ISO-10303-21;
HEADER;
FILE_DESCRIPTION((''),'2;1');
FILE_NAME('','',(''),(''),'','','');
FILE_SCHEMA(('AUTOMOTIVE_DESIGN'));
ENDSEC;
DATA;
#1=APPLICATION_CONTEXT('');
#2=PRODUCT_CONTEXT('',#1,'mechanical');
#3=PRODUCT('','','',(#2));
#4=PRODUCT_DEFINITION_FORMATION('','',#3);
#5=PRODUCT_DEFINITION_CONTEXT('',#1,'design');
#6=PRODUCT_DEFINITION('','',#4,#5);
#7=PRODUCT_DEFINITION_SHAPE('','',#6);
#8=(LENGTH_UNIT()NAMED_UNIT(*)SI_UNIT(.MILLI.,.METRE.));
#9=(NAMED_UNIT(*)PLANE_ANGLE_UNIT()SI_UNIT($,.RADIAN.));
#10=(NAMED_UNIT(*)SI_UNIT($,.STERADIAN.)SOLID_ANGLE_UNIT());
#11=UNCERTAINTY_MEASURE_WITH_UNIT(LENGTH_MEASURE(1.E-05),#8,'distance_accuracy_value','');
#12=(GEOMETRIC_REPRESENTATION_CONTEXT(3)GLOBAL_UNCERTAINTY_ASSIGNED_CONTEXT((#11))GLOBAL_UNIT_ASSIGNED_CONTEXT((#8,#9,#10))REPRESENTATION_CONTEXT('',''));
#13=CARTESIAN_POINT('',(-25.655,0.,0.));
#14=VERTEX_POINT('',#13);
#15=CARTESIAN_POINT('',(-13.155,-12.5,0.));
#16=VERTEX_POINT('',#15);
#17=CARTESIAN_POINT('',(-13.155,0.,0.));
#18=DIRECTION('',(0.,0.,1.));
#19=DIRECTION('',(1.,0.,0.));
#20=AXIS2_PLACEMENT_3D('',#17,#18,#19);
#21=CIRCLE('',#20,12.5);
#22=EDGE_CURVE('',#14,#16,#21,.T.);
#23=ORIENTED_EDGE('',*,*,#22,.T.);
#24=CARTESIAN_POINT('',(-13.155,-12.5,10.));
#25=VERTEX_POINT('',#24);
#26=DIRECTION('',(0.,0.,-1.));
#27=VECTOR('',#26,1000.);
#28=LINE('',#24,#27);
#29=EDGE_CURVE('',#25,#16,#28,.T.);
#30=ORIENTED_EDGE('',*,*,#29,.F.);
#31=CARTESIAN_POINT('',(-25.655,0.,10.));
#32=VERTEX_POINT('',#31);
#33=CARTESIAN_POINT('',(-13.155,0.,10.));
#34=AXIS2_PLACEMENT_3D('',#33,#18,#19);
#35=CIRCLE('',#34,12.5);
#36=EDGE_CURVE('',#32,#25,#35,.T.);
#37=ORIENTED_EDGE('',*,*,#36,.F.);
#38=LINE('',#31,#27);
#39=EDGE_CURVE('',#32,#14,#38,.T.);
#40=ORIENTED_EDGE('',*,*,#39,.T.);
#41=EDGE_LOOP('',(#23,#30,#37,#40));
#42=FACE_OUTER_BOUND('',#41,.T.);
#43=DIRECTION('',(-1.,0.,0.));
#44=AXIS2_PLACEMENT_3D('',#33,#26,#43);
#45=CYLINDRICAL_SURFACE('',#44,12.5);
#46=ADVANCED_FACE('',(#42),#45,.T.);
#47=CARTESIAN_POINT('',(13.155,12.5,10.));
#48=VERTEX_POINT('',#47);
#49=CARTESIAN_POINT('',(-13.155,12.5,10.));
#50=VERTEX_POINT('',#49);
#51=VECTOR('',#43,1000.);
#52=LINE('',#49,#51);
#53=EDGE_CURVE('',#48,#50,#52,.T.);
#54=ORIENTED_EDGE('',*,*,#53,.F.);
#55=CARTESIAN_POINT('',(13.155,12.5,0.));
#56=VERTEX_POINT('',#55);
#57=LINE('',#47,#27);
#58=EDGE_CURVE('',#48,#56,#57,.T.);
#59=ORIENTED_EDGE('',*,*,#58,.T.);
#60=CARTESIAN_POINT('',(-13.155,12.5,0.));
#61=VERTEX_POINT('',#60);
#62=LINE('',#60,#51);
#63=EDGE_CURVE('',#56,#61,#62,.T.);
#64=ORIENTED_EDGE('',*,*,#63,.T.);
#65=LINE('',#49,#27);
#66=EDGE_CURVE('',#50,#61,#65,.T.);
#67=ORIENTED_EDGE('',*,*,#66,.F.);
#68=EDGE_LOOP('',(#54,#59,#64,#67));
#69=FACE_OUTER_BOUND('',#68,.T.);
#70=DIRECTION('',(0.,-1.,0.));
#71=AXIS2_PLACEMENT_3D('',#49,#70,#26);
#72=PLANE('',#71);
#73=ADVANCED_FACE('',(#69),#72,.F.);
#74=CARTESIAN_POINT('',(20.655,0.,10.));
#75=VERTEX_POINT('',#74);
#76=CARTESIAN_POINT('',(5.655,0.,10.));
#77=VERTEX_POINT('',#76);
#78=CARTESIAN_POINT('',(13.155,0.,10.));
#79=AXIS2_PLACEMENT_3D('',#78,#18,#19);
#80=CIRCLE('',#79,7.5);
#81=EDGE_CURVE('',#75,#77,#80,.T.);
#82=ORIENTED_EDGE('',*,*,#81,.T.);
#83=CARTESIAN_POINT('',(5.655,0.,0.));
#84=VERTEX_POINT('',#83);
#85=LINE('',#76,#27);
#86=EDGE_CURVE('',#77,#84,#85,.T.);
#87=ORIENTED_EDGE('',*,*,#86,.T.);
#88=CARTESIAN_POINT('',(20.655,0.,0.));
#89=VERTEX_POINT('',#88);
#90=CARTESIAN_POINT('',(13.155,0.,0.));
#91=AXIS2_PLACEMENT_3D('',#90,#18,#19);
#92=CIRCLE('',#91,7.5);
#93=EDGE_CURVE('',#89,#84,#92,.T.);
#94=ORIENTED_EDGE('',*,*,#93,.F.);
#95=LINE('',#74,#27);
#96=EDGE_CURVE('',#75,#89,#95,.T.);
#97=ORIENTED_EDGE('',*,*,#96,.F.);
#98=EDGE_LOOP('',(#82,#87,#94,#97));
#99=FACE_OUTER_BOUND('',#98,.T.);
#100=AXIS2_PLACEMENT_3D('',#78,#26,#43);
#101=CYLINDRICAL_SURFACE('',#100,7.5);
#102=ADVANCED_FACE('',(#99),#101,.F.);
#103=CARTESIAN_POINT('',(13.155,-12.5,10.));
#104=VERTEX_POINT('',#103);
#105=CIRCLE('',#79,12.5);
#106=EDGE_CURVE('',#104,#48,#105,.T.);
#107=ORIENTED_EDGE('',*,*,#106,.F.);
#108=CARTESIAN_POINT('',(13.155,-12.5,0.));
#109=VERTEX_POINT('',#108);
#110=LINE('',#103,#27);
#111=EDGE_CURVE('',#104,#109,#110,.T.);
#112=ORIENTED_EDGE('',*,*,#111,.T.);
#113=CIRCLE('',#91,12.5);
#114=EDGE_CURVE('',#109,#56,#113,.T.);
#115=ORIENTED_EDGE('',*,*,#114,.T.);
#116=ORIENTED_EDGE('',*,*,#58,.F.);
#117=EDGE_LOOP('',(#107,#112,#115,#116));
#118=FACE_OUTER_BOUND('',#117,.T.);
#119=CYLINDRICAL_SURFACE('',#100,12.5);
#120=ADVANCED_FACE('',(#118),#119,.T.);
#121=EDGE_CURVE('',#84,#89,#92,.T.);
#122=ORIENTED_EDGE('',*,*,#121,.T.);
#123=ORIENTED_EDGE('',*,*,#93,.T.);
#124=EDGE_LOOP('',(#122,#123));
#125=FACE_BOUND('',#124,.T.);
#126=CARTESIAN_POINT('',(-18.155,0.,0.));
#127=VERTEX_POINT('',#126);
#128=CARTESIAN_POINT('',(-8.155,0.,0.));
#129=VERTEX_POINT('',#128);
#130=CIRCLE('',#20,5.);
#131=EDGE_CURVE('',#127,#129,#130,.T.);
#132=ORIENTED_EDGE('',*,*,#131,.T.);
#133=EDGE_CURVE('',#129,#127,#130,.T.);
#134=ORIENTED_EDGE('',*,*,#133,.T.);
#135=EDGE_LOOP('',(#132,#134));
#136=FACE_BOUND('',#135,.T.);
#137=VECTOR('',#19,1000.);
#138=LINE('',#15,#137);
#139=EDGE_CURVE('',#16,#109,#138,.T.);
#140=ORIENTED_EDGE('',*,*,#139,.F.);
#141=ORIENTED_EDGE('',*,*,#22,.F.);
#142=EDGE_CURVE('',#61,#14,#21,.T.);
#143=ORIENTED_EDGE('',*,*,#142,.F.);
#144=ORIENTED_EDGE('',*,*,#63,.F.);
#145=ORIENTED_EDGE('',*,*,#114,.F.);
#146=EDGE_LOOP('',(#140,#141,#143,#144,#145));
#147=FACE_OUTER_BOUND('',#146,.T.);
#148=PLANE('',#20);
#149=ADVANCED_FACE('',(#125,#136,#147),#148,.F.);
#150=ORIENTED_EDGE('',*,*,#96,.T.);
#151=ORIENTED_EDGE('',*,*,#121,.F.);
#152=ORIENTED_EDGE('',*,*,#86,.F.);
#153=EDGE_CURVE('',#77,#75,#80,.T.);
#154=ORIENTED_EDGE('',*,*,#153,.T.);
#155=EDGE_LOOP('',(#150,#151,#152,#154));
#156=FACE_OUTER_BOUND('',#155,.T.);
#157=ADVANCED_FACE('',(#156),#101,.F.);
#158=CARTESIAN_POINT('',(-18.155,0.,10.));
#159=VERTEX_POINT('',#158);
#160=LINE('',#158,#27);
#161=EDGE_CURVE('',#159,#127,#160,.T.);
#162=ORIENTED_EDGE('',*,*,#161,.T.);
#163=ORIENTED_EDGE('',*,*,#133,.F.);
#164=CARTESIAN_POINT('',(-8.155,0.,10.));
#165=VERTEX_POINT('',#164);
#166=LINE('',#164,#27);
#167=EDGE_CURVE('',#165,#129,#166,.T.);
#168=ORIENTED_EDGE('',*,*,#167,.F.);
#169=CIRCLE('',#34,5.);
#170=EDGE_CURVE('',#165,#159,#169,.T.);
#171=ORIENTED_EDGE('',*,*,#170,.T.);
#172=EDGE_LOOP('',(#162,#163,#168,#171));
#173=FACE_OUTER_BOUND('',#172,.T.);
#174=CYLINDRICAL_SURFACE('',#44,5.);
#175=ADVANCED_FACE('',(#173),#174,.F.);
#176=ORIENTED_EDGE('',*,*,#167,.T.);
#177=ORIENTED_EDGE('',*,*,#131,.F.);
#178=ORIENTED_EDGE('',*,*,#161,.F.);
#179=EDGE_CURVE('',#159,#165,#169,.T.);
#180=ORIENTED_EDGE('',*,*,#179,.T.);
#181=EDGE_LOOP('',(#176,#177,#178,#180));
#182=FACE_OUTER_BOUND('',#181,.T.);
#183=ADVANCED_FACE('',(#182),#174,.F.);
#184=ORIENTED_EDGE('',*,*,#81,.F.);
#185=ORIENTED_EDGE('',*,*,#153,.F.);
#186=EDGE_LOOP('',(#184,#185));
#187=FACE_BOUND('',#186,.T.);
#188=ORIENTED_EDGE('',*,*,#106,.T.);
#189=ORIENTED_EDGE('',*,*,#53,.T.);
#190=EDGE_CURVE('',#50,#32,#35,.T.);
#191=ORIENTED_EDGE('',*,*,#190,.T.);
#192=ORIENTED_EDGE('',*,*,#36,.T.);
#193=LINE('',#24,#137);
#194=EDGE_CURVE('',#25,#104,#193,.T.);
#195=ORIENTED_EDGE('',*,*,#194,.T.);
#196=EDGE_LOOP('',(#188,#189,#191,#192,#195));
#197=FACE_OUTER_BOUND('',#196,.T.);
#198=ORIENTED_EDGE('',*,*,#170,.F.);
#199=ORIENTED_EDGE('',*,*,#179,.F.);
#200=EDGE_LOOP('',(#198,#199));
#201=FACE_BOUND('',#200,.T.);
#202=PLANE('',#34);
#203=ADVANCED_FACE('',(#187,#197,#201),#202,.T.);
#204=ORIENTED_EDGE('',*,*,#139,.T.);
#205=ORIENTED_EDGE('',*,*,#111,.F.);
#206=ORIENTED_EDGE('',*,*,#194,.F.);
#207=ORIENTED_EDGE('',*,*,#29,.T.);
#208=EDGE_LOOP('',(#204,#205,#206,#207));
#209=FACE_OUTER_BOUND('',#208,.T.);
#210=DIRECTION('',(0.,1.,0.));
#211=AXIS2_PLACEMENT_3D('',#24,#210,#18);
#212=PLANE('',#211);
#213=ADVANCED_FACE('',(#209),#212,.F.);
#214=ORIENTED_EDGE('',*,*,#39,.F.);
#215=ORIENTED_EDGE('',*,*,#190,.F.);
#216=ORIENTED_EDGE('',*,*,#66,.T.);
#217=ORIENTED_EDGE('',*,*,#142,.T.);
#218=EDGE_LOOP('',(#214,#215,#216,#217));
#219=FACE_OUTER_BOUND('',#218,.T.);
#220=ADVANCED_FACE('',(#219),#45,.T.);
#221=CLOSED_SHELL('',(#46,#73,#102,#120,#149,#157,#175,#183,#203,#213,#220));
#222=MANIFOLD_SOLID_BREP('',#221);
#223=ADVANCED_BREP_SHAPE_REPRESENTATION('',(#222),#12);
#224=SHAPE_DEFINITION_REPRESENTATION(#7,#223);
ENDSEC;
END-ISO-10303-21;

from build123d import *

# Parameters (mm, degrees)
SKETCH_1_R      = 7.5
SKETCH_1_R_2    = 5
EXTRUDE_1_DEPTH = 10


with BuildPart() as part:
    # 草图1 → 凸台-拉伸1 (new body)
    with BuildSketch(Plane.XY):
        with BuildLine():
            Line((-13.155, 12.5), (13.155, 12.5))
            ThreePointArc((13.155, 12.5), (25.655, 0), (13.155, -12.5))
            Line((13.155, -12.5), (-13.155, -12.5))
            ThreePointArc((-13.155, -12.5), (-25.655, 0), (-13.155, 12.5))
        make_face()
        with Locations((13.155, 0)):
            Circle(SKETCH_1_R, mode=Mode.SUBTRACT)
        with Locations((-13.155, 0)):
            Circle(SKETCH_1_R_2, mode=Mode.SUBTRACT)
    extrude(amount=EXTRUDE_1_DEPTH)


solid = part.part
